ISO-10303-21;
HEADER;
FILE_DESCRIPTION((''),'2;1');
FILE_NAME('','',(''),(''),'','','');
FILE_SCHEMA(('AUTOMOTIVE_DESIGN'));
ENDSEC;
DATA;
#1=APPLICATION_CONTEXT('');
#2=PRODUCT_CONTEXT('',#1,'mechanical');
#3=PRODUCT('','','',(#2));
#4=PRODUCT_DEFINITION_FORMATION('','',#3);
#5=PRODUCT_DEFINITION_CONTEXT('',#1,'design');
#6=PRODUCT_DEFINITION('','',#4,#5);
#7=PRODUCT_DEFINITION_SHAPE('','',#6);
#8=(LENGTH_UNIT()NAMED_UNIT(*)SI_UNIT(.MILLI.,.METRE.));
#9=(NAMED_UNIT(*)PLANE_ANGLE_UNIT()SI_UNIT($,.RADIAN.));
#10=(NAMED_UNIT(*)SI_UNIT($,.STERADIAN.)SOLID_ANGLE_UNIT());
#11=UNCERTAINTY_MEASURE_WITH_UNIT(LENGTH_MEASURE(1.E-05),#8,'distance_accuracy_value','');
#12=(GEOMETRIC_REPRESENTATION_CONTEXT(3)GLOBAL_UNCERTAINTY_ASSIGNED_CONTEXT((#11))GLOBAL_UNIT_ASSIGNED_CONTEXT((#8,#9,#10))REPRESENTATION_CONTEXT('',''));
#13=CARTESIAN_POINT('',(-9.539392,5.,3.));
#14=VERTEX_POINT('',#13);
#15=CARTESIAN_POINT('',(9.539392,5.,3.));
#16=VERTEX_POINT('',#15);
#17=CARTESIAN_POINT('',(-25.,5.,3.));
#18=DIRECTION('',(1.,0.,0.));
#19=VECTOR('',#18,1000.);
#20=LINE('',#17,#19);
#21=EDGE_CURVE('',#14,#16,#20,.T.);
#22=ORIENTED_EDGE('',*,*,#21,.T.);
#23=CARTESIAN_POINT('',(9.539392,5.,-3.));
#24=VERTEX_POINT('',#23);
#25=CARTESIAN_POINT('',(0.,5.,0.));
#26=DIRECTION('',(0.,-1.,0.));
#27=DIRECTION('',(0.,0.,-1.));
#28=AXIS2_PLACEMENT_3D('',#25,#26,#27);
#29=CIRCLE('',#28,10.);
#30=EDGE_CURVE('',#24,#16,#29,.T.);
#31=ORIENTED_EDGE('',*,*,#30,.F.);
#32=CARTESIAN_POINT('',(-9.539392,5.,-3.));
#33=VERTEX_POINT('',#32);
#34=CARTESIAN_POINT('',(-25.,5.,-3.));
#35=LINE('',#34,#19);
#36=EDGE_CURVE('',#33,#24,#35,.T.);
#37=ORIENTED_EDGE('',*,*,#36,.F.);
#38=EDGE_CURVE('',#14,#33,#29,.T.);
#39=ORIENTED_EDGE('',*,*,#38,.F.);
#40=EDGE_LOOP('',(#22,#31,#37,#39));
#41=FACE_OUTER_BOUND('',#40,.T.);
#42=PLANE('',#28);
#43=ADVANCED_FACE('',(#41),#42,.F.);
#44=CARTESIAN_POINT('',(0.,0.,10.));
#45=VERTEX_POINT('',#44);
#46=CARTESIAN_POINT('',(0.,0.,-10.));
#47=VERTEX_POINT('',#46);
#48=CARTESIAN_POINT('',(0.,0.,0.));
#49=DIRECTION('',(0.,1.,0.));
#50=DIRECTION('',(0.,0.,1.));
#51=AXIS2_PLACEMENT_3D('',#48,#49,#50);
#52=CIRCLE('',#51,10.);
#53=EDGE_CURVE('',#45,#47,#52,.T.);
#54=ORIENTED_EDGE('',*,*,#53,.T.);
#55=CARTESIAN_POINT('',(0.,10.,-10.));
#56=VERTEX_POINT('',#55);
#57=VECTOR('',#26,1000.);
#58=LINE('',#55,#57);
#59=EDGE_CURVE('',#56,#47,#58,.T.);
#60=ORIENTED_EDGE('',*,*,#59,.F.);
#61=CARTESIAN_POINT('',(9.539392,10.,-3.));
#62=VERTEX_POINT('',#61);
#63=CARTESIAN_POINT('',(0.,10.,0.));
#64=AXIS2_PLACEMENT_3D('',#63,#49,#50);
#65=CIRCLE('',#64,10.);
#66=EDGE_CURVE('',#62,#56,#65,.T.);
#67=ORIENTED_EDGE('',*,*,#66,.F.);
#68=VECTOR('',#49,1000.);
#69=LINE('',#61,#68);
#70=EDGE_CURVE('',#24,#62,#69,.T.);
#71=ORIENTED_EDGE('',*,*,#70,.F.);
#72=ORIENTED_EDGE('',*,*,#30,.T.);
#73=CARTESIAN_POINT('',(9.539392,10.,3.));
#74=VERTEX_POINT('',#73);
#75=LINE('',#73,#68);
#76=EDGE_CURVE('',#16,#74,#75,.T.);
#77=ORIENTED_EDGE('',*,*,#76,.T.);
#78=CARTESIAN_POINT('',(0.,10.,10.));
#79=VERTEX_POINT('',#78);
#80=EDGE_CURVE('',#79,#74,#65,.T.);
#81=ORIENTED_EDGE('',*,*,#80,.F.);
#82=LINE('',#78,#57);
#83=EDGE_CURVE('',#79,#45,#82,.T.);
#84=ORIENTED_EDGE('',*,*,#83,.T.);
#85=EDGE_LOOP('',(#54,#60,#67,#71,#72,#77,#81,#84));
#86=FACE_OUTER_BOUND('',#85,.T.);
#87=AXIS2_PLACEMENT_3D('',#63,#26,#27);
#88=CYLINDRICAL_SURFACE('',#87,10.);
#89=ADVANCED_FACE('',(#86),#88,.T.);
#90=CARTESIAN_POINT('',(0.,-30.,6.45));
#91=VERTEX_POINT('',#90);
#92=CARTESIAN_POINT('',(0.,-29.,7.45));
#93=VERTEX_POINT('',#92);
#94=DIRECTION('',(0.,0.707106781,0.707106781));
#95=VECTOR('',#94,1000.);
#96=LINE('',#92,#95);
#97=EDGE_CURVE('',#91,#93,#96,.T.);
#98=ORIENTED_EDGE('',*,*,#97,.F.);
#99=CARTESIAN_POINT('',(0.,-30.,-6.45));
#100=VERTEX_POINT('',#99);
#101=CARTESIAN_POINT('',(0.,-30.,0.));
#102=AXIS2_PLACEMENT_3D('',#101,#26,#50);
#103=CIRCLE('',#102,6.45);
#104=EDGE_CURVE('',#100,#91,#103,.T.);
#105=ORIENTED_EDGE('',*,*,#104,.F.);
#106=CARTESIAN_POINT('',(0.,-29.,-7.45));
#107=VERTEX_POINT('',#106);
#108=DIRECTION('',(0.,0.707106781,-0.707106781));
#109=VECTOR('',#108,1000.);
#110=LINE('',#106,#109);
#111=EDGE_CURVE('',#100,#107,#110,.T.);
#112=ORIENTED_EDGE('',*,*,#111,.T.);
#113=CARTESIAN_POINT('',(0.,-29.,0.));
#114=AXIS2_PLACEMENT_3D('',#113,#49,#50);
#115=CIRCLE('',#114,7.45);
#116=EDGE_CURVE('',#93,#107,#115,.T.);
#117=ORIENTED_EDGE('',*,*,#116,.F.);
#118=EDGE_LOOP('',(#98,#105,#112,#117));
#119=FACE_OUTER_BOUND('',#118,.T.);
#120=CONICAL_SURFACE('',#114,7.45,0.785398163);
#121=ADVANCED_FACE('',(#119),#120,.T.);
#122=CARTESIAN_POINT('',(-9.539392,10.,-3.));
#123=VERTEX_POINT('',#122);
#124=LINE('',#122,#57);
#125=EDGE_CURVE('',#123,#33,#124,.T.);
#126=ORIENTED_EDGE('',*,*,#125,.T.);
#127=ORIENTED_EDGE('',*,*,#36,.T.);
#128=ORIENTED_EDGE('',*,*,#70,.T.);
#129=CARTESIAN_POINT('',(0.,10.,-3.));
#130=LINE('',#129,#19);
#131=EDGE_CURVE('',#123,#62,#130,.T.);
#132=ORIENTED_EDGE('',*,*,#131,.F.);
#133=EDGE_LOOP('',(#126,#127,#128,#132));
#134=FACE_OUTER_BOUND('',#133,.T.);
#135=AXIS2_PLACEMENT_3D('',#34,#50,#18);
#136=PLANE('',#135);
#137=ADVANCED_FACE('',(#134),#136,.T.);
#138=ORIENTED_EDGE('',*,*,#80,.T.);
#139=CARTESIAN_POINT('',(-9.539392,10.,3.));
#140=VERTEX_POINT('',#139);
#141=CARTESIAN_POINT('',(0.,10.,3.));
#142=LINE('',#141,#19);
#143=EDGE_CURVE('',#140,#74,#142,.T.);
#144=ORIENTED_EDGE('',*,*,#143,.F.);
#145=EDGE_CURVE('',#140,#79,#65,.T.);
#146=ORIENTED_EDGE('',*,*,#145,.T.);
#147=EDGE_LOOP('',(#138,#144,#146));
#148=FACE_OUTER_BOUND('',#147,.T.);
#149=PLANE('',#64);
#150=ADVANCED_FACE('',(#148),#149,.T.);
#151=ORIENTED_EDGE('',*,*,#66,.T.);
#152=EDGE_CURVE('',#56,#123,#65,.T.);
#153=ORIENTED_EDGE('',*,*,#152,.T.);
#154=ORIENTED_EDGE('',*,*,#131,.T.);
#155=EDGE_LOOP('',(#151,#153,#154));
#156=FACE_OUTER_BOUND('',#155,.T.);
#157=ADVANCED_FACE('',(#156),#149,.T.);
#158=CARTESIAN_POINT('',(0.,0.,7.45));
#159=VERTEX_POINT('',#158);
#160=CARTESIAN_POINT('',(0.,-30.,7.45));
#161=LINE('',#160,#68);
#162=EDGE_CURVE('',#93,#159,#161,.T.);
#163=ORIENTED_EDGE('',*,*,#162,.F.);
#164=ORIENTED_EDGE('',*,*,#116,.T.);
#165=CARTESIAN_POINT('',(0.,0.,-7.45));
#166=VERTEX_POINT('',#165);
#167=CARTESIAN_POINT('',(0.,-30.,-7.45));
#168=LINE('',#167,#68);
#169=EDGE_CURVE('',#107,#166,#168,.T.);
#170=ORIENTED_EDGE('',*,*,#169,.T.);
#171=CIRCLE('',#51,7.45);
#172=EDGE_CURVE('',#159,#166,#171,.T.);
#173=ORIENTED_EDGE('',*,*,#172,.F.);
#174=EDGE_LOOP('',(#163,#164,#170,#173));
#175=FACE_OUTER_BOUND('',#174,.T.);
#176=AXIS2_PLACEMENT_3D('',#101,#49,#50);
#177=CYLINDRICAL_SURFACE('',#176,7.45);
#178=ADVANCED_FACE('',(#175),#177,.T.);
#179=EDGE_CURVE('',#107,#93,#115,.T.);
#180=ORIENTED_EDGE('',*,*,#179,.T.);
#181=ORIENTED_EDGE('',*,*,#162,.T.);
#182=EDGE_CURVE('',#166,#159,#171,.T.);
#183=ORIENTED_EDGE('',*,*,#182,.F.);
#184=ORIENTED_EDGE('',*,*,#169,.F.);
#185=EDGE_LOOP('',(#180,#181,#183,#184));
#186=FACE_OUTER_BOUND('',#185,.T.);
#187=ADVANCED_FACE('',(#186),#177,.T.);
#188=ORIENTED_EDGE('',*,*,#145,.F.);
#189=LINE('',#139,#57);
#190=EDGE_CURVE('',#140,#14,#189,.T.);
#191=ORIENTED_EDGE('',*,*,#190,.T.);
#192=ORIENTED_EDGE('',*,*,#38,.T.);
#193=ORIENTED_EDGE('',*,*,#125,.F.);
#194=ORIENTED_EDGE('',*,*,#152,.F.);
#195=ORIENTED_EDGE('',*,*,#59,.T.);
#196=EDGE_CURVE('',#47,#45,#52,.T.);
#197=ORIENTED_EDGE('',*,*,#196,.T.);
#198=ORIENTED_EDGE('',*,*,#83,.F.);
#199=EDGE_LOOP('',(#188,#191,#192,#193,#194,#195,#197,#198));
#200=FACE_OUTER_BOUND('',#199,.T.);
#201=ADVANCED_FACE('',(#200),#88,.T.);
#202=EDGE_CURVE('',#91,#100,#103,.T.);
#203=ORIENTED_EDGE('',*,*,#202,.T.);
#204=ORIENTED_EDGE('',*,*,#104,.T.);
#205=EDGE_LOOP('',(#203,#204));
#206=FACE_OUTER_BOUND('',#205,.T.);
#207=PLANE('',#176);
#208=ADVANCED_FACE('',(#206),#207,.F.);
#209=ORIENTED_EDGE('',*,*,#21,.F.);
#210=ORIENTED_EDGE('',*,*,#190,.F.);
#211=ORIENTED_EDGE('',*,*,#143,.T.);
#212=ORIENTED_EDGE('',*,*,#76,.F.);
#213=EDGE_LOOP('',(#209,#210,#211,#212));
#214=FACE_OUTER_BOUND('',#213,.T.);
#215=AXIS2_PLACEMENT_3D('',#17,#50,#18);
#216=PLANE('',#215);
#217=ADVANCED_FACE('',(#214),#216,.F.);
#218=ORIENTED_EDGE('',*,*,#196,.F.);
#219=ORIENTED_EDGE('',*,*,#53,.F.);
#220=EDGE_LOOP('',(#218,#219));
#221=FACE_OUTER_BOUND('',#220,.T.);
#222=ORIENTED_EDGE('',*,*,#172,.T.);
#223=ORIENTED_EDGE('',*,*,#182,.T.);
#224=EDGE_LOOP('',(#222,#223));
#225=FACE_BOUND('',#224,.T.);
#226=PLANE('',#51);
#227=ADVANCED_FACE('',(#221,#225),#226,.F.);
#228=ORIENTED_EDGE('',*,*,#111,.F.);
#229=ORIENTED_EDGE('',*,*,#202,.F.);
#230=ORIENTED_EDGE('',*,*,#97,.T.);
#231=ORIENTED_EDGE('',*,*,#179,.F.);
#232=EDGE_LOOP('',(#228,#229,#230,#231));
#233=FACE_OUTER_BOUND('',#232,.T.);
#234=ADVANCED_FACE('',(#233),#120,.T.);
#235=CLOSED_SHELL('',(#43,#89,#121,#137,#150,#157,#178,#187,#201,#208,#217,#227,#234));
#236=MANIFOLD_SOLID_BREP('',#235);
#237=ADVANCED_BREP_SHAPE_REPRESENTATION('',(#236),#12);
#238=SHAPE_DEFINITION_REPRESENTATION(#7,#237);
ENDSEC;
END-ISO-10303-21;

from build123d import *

# Parameters (mm, degrees)
SKETCH_1_R          = 7.45
EXTRUDE_1_DEPTH     = 30
SKETCH_2_R          = 10
EXTRUDE_2_DEPTH     = 10
SKETCH_4_W          = 50
SKETCH_4_H          = 6
CUT_EXTRUDE_2_DEPTH = 5
CHAMFER_1_SIZE      = 1


with BuildPart() as part:
    # 草图1 → 凸台-拉伸1 (new body)
    with BuildSketch(Plane(origin=(0, 0, 0), x_dir=(1, 0, 0), z_dir=(0, 1, 0))):
        with Locations(Location((0, 0, 0), (0, 0, 270))):
            Circle(SKETCH_1_R)
    extrude(amount=-EXTRUDE_1_DEPTH)

    # 草图2 → 凸台-拉伸2 (add)
    with BuildSketch(Plane(origin=(0, 0, 0), x_dir=(1, 0, 0), z_dir=(0, 1, 0))):
        with Locations(Location((0, 0, 0), (0, 0, 270))):
            Circle(SKETCH_2_R)
    extrude(amount=EXTRUDE_2_DEPTH)

    # 草图4 → 切除-拉伸2 (cut)
    with BuildSketch(Plane(origin=(0, 10, 0), x_dir=(1, 0, 0), z_dir=(0, 1, 0))):
        Rectangle(SKETCH_4_W, SKETCH_4_H)
    extrude(amount=-CUT_EXTRUDE_2_DEPTH, mode=Mode.SUBTRACT)

    # 倒角1
    chamfer_1_edges = [part.edges().sort_by_distance(p)[0] for p in [
        (0, -30, -7.45),
    ]]
    chamfer(chamfer_1_edges, length=CHAMFER_1_SIZE)


solid = part.part
